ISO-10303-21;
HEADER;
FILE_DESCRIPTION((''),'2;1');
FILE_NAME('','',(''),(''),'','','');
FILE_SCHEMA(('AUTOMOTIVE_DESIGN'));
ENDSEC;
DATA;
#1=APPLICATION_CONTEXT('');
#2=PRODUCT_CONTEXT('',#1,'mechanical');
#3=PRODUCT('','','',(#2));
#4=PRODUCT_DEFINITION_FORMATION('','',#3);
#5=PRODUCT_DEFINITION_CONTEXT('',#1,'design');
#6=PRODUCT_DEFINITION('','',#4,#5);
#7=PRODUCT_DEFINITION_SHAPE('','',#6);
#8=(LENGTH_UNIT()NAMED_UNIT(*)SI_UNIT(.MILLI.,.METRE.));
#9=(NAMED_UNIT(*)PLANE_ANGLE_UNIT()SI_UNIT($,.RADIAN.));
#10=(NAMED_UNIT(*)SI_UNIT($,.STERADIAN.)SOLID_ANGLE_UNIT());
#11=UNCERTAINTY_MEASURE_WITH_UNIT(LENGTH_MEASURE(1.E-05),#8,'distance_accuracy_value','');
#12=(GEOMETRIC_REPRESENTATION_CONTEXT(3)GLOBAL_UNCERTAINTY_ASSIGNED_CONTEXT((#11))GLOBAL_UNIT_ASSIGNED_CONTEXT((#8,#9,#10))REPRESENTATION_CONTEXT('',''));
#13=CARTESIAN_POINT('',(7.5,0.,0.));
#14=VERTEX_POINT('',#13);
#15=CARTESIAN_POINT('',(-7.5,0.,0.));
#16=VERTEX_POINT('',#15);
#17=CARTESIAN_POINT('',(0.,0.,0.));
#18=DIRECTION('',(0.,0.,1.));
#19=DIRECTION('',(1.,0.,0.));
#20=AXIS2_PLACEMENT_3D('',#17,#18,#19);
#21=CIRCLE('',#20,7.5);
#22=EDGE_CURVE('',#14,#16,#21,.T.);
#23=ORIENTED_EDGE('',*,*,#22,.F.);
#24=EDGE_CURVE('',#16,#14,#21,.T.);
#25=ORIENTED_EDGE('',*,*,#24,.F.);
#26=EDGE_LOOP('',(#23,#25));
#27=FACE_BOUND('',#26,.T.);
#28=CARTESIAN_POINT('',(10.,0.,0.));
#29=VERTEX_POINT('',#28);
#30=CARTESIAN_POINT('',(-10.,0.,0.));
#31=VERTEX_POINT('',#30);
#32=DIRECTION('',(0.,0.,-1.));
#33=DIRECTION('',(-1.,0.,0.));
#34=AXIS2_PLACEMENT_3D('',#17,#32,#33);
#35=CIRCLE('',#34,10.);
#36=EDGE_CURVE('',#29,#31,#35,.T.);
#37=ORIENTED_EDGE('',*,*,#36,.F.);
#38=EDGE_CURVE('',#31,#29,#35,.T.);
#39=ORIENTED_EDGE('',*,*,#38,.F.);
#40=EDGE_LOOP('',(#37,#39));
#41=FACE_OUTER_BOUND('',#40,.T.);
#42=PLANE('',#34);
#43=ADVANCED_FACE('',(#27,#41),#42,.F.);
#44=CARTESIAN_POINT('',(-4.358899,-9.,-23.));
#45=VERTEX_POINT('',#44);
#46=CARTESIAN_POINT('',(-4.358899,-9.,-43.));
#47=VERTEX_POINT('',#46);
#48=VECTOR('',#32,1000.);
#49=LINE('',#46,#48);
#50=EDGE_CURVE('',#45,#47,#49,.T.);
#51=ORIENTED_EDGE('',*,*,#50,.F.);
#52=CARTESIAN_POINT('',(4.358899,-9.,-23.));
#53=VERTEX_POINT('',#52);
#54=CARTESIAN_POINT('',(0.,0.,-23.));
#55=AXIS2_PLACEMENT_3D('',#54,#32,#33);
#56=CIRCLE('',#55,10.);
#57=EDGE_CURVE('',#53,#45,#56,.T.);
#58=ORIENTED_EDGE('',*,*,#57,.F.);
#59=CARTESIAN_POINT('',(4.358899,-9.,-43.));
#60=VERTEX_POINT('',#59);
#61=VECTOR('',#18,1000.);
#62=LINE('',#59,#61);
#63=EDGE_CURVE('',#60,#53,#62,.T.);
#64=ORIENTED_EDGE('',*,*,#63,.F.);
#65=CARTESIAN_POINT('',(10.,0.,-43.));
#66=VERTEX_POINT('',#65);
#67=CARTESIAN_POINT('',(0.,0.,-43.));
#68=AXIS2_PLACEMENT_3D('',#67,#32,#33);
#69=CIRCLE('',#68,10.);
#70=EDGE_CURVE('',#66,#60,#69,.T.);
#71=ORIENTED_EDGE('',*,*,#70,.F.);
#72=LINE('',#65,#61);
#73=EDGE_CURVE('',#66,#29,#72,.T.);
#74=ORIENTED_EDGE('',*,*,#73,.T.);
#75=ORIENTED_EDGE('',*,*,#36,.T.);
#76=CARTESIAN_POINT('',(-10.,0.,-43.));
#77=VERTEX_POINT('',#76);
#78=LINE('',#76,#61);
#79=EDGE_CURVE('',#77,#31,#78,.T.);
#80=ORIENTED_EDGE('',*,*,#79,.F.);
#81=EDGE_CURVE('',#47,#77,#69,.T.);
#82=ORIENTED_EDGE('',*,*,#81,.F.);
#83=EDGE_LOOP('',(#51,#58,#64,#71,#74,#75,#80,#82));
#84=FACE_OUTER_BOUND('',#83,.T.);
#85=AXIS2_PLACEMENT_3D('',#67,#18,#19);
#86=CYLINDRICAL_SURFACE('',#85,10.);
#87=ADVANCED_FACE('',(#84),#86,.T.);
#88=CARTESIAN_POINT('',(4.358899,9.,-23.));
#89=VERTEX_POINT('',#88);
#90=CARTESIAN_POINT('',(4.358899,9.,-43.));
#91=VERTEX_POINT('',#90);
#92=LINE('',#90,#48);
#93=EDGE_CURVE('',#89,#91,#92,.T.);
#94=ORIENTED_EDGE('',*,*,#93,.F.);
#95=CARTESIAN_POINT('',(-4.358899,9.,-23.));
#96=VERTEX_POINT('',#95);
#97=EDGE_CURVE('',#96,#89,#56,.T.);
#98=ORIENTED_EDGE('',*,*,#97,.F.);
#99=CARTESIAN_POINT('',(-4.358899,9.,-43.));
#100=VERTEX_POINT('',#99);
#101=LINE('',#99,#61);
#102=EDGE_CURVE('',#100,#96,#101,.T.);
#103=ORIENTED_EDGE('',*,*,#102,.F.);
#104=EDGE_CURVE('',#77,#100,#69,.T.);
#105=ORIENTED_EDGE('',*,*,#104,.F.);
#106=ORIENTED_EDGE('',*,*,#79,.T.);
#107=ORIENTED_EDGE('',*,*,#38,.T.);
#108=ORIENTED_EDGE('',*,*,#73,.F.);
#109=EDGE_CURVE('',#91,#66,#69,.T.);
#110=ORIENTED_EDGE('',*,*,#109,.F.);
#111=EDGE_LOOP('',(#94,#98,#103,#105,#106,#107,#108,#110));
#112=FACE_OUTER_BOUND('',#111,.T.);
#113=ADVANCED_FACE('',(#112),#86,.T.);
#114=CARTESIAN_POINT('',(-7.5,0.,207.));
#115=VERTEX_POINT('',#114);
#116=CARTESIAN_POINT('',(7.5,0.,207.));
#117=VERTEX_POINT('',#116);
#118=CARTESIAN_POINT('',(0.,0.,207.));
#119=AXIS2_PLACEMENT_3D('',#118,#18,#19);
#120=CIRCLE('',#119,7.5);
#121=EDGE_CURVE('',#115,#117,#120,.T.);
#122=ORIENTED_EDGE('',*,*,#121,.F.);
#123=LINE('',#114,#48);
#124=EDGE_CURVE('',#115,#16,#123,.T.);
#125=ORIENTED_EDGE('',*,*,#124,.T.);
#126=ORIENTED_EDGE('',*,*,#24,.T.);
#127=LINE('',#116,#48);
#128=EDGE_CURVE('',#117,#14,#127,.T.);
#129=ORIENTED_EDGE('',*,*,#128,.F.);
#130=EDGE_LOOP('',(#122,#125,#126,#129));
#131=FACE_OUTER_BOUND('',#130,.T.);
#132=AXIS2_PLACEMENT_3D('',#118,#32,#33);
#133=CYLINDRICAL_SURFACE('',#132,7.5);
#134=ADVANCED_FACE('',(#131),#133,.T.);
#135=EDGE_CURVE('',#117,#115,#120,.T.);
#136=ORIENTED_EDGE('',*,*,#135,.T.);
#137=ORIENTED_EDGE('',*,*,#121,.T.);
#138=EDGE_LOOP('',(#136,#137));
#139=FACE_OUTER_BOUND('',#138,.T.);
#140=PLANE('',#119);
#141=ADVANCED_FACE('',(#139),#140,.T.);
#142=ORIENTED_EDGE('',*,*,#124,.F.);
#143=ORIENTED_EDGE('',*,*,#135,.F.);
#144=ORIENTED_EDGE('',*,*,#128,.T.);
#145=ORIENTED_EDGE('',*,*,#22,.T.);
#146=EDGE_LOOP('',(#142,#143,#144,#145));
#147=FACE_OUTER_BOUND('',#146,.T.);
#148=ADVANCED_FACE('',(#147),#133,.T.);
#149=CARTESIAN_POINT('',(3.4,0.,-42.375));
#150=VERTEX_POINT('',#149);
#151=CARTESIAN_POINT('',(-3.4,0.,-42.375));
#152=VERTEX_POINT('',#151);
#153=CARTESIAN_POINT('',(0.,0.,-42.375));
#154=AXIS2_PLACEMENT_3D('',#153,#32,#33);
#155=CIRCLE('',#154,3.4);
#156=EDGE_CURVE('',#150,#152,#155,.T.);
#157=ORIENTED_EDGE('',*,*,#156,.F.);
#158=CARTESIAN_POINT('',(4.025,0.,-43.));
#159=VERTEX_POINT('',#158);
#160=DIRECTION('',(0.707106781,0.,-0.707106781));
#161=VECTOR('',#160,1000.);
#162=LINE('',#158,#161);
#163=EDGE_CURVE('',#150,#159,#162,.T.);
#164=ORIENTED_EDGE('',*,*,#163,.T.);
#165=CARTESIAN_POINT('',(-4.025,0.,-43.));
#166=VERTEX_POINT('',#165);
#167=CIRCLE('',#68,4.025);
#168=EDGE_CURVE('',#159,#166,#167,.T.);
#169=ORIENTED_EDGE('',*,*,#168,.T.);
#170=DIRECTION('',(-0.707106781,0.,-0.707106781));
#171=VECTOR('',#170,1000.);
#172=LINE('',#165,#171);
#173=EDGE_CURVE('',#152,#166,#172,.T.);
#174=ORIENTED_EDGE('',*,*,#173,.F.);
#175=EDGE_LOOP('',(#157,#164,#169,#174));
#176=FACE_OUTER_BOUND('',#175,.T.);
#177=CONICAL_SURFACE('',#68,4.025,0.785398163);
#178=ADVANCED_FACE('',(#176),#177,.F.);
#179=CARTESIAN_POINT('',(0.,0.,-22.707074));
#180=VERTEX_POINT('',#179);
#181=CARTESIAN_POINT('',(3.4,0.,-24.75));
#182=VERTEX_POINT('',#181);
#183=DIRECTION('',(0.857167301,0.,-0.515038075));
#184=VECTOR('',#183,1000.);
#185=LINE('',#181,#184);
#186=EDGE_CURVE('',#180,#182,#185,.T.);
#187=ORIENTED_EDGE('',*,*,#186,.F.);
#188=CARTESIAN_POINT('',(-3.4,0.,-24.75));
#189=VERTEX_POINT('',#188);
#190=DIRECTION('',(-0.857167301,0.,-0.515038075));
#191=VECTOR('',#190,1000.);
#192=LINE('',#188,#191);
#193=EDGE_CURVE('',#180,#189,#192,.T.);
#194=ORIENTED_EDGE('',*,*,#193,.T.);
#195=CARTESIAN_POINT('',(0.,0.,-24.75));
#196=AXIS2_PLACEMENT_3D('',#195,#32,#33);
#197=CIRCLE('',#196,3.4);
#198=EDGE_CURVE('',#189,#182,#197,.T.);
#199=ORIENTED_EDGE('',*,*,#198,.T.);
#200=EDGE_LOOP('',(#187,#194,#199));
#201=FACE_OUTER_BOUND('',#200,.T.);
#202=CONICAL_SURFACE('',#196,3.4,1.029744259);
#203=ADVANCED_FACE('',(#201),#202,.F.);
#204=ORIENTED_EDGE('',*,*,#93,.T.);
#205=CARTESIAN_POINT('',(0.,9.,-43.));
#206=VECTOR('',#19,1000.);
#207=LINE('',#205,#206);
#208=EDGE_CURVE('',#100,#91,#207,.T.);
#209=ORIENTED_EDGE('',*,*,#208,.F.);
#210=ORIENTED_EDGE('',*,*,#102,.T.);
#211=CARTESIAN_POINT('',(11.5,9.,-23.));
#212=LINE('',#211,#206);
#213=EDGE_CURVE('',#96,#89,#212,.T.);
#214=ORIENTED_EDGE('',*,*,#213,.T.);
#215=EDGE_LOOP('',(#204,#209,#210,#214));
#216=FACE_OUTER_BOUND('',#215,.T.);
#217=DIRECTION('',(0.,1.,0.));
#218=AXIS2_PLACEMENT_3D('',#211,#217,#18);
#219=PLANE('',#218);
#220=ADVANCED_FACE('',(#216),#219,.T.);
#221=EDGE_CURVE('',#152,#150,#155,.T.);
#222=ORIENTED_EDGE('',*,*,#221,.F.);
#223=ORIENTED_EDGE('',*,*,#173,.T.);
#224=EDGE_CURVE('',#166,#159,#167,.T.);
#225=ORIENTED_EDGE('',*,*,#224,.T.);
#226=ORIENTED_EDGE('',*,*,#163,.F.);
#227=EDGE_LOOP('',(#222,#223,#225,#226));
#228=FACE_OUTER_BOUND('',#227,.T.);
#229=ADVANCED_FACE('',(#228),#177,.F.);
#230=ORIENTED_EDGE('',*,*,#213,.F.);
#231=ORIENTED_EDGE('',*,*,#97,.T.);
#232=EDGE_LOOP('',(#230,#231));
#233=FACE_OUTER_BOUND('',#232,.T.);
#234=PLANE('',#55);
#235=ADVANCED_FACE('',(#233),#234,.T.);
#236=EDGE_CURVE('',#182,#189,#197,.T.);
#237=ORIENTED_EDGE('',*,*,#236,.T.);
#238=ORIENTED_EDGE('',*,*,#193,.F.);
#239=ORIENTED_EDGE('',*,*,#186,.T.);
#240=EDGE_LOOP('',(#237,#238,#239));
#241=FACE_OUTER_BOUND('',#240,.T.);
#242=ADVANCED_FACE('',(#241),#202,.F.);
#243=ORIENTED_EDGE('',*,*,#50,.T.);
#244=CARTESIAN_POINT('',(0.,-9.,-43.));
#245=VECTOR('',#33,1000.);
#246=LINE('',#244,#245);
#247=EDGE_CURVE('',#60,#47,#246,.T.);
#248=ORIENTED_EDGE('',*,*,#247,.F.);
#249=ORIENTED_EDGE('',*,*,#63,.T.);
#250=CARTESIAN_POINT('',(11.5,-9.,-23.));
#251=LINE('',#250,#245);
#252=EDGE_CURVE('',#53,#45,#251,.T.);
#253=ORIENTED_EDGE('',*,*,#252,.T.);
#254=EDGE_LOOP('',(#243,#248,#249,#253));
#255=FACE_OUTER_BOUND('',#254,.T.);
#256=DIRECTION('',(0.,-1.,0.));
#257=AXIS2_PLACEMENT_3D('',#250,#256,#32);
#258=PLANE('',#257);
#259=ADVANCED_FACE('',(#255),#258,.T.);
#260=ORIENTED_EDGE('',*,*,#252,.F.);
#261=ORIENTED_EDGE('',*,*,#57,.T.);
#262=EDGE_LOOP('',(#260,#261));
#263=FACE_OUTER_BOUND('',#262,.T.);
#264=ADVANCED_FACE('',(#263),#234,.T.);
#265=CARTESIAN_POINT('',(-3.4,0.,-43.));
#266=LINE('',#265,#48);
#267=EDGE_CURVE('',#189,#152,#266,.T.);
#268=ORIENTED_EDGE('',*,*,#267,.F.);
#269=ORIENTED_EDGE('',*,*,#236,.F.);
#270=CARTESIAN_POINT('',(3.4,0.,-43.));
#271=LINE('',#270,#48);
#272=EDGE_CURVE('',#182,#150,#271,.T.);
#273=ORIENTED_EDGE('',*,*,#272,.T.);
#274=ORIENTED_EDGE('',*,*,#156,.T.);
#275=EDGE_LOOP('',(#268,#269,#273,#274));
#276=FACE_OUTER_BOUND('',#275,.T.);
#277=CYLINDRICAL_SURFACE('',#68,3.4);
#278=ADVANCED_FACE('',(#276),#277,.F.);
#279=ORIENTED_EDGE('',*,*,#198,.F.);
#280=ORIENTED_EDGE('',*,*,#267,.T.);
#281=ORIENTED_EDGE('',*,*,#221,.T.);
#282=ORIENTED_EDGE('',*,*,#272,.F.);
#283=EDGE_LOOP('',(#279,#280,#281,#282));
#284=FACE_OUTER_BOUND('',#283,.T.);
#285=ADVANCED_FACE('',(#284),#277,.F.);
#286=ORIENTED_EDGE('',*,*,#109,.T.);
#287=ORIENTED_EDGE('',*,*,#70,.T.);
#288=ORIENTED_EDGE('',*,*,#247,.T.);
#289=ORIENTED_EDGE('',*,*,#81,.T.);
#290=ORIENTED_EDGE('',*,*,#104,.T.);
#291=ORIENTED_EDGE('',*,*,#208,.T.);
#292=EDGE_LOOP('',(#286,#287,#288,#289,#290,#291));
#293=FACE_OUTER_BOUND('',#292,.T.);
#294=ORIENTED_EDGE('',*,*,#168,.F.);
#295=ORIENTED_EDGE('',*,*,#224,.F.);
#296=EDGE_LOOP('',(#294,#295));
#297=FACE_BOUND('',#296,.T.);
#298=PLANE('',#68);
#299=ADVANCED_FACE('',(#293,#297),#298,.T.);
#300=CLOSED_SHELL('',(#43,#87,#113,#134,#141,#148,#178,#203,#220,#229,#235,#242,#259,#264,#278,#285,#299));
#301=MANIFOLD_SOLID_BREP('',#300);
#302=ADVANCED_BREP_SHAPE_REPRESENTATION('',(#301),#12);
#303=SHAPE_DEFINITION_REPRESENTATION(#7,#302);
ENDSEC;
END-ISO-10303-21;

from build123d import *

# Parameters (mm, degrees)
SKETCH_1_R                   = 7.5
EXTRUDE_1_DEPTH              = 207
SKETCH_2_R                   = 10
EXTRUDE_2_DEPTH              = 43
SKETCH_3_OUTSIDE_W           = 72.318
SKETCH_3_OUTSIDE_H           = 72.318
SKETCH_3_OUTSIDE_W_2         = 23
SKETCH_3_OUTSIDE_H_2         = 18
CUT_EXTRUDE_1_DEPTH          = 20
HOLE_WIZARD_M8_1_D           = 6.8
HOLE_WIZARD_M8_1_DEPTH       = 18.25
HOLE_WIZARD_M8_1_CSINK_D     = 8.05
HOLE_WIZARD_M8_1_CSINK_ANGLE = 90
HOLE_WIZARD_M8_1_TIP         = 2.042926105


with BuildPart() as part:
    # 草图1 → 凸台-拉伸1 (new body)
    with BuildSketch(Plane.XY):
        Circle(SKETCH_1_R)
    extrude(amount=EXTRUDE_1_DEPTH)

    # 草图2 → 凸台-拉伸2 (add)
    with BuildSketch(Plane(origin=(0, 0, 0), x_dir=(-1, 0, 0), z_dir=(0, 0, -1))):
        Circle(SKETCH_2_R)
    extrude(amount=EXTRUDE_2_DEPTH)

    # 草图3 outside → 切除-拉伸1 (cut)
    with BuildSketch(Plane(origin=(0, 0, -43), x_dir=(-1, 0, 0), z_dir=(0, 0, -1))):
        Rectangle(SKETCH_3_OUTSIDE_W, SKETCH_3_OUTSIDE_H)
        Rectangle(SKETCH_3_OUTSIDE_W_2, SKETCH_3_OUTSIDE_H_2, mode=Mode.SUBTRACT)
    extrude(amount=-CUT_EXTRUDE_1_DEPTH, mode=Mode.SUBTRACT)

    # M8 螺纹孔1
    with Locations(Plane(origin=(0, 0, -43), x_dir=(-1, 0, 0), z_dir=(0, 0, -1))):
        with Locations((0, 0)):
            CounterSinkHole(HOLE_WIZARD_M8_1_D / 2, HOLE_WIZARD_M8_1_CSINK_D / 2, depth=HOLE_WIZARD_M8_1_DEPTH, counter_sink_angle=HOLE_WIZARD_M8_1_CSINK_ANGLE)
            with Locations((0, 0, -(HOLE_WIZARD_M8_1_DEPTH + HOLE_WIZARD_M8_1_TIP / 2))):  # 118° drill point
                Cone(0, HOLE_WIZARD_M8_1_D / 2, HOLE_WIZARD_M8_1_TIP, mode=Mode.SUBTRACT)


solid = part.part
